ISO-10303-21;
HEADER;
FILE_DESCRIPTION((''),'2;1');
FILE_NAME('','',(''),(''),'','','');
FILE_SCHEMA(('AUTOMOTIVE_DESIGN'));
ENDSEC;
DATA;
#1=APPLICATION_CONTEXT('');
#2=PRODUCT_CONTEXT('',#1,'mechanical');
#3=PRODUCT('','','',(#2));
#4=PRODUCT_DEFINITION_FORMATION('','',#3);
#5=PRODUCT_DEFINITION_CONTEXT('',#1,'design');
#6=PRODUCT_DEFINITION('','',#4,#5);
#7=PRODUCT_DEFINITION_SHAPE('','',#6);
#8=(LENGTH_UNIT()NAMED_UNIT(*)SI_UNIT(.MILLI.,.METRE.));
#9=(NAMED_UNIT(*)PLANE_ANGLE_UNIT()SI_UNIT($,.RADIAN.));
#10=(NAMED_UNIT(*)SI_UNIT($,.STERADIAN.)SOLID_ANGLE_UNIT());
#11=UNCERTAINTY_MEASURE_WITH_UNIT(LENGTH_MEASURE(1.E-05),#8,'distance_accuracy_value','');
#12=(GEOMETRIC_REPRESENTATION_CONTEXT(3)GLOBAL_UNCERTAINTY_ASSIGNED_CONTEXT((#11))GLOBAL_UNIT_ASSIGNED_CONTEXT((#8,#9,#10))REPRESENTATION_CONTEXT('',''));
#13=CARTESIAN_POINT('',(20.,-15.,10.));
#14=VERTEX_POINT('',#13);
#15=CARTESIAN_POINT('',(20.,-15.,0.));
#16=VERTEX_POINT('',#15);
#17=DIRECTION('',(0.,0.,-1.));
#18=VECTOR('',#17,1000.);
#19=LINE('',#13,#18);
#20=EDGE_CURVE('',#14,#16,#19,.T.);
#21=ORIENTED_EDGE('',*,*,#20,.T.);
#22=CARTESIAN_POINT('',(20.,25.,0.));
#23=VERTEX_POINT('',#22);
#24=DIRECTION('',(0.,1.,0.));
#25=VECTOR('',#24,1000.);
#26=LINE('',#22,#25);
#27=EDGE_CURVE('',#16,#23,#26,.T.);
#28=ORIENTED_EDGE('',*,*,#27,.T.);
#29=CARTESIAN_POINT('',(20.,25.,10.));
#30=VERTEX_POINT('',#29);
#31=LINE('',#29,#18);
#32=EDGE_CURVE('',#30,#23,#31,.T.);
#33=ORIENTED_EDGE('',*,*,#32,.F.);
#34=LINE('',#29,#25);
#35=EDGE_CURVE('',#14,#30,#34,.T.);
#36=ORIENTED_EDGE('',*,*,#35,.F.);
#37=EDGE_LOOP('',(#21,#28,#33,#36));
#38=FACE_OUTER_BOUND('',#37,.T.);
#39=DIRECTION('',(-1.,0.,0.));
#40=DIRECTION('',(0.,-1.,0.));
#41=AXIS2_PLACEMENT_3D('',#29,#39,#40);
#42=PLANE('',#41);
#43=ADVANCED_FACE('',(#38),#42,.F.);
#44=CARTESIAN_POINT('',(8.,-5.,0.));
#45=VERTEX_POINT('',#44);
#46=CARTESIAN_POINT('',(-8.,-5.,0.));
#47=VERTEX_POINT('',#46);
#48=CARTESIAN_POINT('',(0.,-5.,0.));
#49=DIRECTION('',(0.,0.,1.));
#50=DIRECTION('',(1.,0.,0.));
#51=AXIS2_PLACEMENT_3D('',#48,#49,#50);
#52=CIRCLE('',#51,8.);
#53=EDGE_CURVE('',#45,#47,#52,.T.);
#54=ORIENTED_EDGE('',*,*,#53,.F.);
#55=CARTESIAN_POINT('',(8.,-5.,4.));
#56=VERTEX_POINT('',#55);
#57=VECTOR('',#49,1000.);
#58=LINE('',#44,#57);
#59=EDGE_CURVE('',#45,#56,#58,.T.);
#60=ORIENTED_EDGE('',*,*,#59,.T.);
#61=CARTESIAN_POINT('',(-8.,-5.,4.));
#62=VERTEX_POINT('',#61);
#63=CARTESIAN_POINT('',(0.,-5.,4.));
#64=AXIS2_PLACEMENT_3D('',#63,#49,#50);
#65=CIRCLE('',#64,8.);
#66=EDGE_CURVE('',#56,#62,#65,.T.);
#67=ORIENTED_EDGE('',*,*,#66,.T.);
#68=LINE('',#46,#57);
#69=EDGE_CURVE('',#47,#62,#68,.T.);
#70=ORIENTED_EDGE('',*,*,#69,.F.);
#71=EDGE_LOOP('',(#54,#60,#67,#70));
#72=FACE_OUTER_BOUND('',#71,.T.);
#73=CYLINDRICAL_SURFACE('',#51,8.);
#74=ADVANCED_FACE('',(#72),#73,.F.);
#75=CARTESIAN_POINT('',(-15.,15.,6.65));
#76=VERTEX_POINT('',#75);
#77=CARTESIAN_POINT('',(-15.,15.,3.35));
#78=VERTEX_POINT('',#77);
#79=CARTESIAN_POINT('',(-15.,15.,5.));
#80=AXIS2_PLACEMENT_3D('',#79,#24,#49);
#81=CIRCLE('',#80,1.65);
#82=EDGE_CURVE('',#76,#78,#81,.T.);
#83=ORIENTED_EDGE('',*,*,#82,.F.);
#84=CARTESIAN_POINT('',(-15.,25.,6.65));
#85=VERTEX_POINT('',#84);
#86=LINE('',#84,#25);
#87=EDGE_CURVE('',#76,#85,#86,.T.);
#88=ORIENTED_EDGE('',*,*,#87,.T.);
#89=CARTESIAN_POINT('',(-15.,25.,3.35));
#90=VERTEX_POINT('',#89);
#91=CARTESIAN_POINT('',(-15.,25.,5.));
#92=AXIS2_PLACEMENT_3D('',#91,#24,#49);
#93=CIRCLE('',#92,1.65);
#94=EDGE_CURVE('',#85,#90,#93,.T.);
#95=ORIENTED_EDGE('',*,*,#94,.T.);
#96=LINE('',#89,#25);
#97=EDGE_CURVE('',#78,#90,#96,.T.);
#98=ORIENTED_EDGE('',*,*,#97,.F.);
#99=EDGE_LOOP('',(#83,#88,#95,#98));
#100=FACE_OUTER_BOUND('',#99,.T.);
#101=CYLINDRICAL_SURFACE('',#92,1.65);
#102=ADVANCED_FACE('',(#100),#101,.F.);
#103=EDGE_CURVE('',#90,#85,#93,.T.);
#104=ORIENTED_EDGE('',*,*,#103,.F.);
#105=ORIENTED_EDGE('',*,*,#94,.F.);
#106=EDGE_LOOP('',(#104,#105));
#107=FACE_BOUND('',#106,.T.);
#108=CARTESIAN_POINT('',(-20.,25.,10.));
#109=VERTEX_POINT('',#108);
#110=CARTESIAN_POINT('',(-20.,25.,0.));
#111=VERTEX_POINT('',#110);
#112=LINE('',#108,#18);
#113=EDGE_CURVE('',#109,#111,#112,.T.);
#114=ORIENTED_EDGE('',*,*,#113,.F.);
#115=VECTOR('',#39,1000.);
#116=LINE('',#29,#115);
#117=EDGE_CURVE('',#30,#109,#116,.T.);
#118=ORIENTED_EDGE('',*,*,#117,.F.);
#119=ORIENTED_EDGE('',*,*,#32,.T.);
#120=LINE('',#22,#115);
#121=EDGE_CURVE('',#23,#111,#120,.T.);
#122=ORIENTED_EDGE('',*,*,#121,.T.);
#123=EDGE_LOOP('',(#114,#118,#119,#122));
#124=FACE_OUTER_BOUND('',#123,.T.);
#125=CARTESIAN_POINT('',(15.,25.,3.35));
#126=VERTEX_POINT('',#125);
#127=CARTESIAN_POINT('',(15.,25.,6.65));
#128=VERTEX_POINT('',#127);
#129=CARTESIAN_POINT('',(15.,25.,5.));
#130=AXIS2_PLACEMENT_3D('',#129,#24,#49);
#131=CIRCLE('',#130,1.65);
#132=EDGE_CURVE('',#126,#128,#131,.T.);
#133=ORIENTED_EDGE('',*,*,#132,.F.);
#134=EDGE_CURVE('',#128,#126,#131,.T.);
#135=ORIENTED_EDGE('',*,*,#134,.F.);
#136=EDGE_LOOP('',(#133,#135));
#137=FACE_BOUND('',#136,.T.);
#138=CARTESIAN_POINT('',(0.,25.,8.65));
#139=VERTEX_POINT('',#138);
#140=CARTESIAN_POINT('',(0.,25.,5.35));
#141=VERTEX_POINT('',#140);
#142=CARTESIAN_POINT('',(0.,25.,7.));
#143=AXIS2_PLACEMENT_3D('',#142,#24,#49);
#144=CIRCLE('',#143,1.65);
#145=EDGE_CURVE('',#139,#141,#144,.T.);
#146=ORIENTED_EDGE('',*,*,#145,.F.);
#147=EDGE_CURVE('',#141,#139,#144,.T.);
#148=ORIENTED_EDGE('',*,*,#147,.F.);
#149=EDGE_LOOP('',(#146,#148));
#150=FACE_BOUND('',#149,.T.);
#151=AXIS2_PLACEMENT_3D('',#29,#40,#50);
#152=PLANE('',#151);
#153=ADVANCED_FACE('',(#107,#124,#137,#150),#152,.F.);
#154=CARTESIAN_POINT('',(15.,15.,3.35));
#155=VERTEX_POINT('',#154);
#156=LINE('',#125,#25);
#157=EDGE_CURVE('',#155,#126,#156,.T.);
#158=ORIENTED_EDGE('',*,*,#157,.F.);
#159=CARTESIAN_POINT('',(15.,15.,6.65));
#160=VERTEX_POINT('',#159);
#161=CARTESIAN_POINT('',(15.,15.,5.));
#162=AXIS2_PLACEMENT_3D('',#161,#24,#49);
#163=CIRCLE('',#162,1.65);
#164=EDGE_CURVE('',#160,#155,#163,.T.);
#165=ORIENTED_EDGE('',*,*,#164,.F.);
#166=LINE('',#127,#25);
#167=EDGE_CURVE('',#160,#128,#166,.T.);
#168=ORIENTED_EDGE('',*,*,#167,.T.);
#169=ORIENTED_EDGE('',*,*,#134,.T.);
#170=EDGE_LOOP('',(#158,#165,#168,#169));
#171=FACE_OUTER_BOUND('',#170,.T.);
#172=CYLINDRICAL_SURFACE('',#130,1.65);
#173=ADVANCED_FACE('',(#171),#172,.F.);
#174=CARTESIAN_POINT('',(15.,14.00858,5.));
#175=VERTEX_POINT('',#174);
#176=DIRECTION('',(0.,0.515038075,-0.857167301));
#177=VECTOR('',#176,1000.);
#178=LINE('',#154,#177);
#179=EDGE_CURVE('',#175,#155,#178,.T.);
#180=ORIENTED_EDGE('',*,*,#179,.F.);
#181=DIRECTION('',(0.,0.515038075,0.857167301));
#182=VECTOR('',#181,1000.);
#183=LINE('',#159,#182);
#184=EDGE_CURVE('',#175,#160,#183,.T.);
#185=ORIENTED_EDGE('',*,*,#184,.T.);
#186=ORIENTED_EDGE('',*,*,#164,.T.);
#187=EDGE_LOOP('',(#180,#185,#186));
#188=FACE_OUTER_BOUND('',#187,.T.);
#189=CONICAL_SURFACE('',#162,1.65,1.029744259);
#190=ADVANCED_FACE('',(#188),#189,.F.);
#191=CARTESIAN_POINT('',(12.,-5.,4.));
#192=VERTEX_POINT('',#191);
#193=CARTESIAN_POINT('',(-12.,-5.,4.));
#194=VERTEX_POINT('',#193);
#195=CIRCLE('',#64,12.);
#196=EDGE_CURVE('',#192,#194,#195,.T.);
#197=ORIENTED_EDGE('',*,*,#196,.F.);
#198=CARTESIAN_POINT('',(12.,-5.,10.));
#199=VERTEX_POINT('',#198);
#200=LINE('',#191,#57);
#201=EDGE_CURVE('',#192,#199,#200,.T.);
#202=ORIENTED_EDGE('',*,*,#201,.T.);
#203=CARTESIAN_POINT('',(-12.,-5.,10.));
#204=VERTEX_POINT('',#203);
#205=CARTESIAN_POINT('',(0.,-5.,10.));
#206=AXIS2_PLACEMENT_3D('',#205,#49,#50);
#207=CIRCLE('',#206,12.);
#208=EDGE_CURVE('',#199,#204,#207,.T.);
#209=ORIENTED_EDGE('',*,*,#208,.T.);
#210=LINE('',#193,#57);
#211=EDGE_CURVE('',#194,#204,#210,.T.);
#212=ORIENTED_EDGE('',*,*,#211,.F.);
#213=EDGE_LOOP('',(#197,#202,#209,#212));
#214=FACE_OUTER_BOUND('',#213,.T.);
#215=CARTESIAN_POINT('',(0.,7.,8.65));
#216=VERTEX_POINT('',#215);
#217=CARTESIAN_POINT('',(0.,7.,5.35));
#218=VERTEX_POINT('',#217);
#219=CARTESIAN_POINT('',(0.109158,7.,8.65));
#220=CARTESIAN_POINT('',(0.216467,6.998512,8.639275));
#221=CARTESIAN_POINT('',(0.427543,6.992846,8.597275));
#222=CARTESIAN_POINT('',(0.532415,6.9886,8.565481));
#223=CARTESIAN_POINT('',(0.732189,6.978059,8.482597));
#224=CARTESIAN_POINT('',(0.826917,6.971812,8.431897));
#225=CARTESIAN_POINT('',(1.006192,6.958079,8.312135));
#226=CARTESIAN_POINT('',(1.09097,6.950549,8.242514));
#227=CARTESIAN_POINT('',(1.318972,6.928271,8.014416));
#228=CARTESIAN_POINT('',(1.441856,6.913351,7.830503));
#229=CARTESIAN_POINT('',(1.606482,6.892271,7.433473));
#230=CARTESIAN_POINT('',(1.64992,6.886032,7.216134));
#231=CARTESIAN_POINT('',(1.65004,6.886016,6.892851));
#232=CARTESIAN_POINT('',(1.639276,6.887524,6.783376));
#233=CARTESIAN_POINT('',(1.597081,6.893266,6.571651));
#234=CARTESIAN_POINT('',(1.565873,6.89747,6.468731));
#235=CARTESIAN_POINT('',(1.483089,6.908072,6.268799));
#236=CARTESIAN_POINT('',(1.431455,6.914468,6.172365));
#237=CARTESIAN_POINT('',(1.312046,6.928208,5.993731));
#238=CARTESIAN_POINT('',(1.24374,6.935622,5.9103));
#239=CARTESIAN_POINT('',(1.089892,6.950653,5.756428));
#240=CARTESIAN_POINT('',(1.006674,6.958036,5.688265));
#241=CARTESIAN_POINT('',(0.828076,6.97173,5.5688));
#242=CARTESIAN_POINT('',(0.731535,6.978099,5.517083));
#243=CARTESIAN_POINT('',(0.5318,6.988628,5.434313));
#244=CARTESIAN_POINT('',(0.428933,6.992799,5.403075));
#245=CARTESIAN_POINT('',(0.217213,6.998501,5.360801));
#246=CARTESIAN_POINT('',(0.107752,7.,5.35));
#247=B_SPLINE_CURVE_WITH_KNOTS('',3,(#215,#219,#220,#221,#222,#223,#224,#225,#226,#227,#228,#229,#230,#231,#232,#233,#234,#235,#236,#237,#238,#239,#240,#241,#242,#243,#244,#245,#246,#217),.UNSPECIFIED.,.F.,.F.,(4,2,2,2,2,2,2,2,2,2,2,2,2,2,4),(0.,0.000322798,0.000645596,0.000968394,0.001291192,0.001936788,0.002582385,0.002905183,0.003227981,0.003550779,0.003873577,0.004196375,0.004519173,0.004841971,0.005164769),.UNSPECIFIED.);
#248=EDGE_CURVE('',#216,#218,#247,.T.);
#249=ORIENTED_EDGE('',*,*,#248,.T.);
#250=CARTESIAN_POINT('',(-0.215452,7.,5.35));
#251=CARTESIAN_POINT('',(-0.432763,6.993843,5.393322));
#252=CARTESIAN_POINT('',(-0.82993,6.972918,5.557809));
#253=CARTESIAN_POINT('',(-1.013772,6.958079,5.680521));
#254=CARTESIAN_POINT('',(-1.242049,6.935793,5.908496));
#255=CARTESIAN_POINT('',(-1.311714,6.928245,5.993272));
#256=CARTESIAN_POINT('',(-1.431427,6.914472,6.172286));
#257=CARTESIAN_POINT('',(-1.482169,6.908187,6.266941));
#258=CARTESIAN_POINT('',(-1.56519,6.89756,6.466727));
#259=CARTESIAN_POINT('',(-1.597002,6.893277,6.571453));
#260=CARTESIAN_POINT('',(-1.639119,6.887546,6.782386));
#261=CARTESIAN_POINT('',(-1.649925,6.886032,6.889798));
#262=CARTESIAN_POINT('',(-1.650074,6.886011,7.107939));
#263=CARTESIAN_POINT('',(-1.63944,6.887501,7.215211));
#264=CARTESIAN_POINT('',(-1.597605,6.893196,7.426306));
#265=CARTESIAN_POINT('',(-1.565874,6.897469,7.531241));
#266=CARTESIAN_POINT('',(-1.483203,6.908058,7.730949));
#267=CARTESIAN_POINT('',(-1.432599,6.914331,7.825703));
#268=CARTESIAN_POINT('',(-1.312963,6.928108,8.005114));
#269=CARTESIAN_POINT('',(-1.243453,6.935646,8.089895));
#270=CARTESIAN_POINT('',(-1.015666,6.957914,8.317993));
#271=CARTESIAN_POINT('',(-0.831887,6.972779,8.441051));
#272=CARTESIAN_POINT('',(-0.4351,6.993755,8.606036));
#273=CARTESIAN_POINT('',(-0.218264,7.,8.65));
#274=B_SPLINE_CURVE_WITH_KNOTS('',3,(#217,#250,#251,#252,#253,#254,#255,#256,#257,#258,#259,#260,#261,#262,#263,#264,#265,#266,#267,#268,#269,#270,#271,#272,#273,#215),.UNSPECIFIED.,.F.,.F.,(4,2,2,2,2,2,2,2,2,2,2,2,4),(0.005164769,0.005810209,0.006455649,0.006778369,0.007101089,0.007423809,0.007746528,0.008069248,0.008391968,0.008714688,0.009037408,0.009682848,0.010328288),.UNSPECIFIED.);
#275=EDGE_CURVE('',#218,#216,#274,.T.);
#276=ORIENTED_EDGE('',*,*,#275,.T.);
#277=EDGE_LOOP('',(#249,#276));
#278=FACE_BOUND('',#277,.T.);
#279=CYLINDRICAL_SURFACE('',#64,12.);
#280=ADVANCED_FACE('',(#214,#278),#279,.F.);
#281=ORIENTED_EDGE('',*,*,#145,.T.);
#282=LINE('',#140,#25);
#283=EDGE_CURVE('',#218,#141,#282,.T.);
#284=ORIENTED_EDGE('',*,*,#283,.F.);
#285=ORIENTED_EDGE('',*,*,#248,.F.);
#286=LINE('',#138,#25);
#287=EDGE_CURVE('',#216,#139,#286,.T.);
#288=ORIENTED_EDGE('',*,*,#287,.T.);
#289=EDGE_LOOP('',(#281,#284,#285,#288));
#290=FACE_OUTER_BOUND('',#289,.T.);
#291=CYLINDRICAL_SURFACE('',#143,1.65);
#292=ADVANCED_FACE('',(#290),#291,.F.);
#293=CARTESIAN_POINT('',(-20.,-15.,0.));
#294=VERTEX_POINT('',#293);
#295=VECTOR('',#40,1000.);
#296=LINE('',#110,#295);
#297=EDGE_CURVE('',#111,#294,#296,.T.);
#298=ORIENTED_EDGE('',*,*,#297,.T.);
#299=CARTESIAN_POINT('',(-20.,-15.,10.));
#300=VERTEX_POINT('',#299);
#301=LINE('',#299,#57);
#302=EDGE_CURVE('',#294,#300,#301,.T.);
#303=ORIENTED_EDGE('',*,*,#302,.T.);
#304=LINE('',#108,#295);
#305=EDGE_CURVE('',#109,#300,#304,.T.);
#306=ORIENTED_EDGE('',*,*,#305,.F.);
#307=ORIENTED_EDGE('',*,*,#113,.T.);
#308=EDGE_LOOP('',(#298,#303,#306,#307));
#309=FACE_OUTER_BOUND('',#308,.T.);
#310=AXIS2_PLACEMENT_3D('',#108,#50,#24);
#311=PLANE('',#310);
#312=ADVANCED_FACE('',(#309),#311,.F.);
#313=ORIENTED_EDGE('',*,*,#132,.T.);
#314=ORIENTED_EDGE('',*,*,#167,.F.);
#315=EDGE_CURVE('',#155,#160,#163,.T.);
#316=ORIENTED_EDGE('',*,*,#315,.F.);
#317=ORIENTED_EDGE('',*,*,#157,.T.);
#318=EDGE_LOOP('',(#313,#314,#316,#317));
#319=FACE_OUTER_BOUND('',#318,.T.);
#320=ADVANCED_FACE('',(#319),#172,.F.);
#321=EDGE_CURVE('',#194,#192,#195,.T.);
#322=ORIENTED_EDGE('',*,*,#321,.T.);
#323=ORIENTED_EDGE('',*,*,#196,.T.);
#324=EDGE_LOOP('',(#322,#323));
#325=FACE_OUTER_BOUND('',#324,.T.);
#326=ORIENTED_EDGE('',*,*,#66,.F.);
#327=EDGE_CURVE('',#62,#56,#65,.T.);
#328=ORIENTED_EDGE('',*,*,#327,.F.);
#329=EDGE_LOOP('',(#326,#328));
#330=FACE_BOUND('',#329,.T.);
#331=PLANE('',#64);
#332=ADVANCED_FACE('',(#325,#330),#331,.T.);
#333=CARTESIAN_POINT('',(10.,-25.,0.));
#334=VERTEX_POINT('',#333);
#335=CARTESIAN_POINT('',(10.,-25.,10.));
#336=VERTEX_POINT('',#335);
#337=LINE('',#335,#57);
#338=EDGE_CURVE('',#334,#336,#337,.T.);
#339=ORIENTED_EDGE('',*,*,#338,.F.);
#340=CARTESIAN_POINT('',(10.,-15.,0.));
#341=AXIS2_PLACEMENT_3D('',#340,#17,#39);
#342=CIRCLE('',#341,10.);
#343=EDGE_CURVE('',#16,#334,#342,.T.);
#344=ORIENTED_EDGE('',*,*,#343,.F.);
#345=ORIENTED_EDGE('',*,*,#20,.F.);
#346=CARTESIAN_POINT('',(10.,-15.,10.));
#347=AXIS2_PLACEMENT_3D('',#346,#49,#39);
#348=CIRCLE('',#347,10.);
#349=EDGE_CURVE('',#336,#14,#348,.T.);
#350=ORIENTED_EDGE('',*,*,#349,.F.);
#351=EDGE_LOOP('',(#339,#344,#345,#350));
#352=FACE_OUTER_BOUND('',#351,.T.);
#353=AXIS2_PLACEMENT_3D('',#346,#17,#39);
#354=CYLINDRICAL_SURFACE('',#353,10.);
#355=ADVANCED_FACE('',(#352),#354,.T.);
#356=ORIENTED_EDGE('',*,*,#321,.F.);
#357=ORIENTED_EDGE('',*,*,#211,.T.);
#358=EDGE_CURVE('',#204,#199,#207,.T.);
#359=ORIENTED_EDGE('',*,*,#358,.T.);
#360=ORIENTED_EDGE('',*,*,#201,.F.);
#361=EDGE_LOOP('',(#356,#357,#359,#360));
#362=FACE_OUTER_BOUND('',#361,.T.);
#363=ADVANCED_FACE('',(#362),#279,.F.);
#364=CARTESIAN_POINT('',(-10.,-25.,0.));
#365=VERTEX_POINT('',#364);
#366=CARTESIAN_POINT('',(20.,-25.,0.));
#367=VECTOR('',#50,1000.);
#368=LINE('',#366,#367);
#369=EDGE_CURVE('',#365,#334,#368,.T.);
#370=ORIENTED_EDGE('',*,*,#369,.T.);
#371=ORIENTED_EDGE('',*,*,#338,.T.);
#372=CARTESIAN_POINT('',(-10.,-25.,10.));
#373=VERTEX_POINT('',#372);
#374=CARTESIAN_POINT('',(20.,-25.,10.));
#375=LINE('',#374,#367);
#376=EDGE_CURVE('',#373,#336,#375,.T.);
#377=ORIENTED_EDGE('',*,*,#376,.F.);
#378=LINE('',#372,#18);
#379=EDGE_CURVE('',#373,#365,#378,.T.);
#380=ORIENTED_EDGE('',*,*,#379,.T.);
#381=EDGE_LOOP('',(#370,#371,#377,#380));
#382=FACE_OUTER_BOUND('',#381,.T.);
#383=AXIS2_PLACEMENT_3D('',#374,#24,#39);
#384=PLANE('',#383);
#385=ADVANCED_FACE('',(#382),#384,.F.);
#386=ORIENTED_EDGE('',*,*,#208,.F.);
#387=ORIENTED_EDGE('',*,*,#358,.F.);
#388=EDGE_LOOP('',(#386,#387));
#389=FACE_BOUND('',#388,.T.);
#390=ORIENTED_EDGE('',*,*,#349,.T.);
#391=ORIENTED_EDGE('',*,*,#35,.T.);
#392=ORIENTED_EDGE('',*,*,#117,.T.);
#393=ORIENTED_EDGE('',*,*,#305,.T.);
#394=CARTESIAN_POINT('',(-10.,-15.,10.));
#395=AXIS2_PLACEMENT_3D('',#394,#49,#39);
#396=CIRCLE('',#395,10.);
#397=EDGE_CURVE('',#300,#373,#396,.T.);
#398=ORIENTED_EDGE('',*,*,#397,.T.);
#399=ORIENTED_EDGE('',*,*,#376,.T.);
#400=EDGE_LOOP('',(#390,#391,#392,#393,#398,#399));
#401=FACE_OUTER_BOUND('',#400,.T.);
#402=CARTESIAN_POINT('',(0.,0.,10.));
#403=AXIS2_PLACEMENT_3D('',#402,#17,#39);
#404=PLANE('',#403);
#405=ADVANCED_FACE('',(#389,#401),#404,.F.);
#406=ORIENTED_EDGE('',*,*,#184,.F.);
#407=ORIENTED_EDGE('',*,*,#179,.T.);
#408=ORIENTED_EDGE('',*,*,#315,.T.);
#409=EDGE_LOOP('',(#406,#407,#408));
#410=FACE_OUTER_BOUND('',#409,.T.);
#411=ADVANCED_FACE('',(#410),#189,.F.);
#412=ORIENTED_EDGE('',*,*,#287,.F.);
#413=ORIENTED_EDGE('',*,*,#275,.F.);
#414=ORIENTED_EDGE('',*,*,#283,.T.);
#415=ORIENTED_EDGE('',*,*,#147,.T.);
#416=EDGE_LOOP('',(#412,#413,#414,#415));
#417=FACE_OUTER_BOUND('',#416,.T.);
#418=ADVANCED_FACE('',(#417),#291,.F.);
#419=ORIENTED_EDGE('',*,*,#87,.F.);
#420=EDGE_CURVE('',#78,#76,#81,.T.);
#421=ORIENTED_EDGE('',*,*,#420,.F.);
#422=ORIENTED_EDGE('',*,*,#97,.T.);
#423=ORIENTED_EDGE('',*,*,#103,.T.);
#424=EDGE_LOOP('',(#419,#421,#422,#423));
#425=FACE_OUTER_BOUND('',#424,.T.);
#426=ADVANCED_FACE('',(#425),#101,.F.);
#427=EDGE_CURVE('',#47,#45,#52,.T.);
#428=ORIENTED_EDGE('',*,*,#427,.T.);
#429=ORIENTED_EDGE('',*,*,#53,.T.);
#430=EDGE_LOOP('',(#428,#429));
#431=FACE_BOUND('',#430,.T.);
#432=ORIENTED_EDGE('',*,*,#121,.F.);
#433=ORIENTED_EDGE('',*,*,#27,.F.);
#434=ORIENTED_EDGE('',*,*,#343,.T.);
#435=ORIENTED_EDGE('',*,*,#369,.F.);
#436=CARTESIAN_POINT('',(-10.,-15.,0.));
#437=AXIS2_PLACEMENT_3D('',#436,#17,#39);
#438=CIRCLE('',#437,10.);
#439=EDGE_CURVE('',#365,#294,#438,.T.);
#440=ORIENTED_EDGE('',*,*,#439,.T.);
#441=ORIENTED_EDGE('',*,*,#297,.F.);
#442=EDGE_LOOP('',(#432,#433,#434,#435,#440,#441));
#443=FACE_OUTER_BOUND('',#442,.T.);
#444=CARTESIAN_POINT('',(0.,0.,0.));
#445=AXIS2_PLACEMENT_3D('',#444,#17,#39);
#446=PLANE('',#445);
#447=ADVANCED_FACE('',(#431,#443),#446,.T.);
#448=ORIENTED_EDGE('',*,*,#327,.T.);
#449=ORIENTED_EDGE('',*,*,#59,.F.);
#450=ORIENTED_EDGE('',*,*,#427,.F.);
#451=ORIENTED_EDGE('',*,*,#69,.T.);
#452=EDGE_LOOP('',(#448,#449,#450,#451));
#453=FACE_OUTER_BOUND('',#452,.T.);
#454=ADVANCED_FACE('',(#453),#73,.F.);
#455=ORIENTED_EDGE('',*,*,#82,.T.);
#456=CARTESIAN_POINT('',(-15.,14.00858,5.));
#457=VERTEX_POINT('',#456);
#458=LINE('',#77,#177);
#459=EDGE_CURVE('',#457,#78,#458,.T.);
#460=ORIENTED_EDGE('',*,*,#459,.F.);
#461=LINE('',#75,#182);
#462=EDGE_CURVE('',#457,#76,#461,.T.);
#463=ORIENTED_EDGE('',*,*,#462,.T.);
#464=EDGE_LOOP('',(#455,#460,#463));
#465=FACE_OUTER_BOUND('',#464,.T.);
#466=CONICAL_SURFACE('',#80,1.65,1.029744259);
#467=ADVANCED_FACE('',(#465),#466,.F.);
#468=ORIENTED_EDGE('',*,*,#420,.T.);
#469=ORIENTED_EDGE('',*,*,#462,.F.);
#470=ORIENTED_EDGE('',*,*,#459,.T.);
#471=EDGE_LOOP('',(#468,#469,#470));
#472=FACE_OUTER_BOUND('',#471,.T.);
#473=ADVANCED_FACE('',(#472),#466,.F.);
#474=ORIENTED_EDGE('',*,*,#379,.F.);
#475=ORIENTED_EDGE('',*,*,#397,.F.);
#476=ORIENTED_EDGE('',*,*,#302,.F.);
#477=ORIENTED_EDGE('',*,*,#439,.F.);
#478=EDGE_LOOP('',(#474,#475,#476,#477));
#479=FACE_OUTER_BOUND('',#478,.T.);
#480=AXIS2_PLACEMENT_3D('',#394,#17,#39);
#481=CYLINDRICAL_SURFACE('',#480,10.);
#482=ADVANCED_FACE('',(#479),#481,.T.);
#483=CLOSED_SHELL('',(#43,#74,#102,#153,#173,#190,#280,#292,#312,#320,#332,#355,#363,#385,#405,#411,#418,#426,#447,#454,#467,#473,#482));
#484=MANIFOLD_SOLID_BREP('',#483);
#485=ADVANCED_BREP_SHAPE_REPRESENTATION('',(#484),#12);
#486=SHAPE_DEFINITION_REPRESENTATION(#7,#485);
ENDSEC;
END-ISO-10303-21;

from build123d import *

# Parameters (mm, degrees)
SKETCH_1_W              = 40
SKETCH_1_H              = 50
EXTRUDE_1_DEPTH         = 10
SKETCH_2_R              = 12
CUT_EXTRUDE_1_DEPTH     = 6
SKETCH_3_R              = 8
CUT_EXTRUDE_2_DEPTH     = 33.57299495
HOLE_WIZARD_M4_1_D      = 3.3
HOLE_WIZARD_M4_1_DEPTH  = 10
HOLE_WIZARD_M4_1_TIP    = 0.991420021
FILLET_1_R              = 10
HOLE_WIZARD_M4_3_REACH  = 56.772
HOLE_WIZARD_M4_3_BORE_R = 1.65


with BuildPart() as part:
    # 草图1 → 凸台-拉伸1 (new body)
    with BuildSketch(Plane.XY):
        Rectangle(SKETCH_1_W, SKETCH_1_H)
    extrude(amount=EXTRUDE_1_DEPTH)

    # 草图2 → 切除-拉伸1 (cut)
    with BuildSketch(Plane.XY.offset(10)):
        with Locations((0, -5)):
            Circle(SKETCH_2_R)
    extrude(amount=-CUT_EXTRUDE_1_DEPTH, mode=Mode.SUBTRACT)

    # 草图3 → 切除-拉伸2 (cut, through all)
    with BuildSketch(Plane.XY.offset(4)):
        with Locations((0, -5)):
            Circle(SKETCH_3_R)
    extrude(amount=-CUT_EXTRUDE_2_DEPTH, mode=Mode.SUBTRACT)

    # M4 螺纹孔1
    with Locations(Plane(origin=(0, 25, 0), x_dir=(1, 0, 0), z_dir=(0, 1, 0))):
        with Locations((-15, -5), (15, -5)):
            Hole(HOLE_WIZARD_M4_1_D / 2, depth=HOLE_WIZARD_M4_1_DEPTH)
            with Locations((0, 0, -(HOLE_WIZARD_M4_1_DEPTH + HOLE_WIZARD_M4_1_TIP / 2))):  # 118° drill point
                Cone(0, HOLE_WIZARD_M4_1_D / 2, HOLE_WIZARD_M4_1_TIP, mode=Mode.SUBTRACT)

    # 圆角1
    fillet_1_edges = [part.edges().sort_by_distance(p)[0] for p in [
        (20, -25, 5),
        (-20, -25, 5),
    ]]
    fillet(fillet_1_edges, radius=FILLET_1_R)

    # M4 螺纹孔3 bore → M4 螺纹孔3 (cut, up to next)
    with BuildSketch(Plane(origin=(0, 25, 0), x_dir=(1, 0, 0), z_dir=(0, 1, 0)), mode=Mode.PRIVATE) as hole_wizard_m4_3_sk1:
        with Locations((0, -7)):
            Circle(HOLE_WIZARD_M4_3_BORE_R)
    hole_wizard_m4_3_tool1 = extrude(hole_wizard_m4_3_sk1.sketch, amount=-HOLE_WIZARD_M4_3_REACH, mode=Mode.PRIVATE) & part.part
    add(hole_wizard_m4_3_tool1.solids().sort_by_distance((0, 25, 7))[0], mode=Mode.SUBTRACT)


solid = part.part
